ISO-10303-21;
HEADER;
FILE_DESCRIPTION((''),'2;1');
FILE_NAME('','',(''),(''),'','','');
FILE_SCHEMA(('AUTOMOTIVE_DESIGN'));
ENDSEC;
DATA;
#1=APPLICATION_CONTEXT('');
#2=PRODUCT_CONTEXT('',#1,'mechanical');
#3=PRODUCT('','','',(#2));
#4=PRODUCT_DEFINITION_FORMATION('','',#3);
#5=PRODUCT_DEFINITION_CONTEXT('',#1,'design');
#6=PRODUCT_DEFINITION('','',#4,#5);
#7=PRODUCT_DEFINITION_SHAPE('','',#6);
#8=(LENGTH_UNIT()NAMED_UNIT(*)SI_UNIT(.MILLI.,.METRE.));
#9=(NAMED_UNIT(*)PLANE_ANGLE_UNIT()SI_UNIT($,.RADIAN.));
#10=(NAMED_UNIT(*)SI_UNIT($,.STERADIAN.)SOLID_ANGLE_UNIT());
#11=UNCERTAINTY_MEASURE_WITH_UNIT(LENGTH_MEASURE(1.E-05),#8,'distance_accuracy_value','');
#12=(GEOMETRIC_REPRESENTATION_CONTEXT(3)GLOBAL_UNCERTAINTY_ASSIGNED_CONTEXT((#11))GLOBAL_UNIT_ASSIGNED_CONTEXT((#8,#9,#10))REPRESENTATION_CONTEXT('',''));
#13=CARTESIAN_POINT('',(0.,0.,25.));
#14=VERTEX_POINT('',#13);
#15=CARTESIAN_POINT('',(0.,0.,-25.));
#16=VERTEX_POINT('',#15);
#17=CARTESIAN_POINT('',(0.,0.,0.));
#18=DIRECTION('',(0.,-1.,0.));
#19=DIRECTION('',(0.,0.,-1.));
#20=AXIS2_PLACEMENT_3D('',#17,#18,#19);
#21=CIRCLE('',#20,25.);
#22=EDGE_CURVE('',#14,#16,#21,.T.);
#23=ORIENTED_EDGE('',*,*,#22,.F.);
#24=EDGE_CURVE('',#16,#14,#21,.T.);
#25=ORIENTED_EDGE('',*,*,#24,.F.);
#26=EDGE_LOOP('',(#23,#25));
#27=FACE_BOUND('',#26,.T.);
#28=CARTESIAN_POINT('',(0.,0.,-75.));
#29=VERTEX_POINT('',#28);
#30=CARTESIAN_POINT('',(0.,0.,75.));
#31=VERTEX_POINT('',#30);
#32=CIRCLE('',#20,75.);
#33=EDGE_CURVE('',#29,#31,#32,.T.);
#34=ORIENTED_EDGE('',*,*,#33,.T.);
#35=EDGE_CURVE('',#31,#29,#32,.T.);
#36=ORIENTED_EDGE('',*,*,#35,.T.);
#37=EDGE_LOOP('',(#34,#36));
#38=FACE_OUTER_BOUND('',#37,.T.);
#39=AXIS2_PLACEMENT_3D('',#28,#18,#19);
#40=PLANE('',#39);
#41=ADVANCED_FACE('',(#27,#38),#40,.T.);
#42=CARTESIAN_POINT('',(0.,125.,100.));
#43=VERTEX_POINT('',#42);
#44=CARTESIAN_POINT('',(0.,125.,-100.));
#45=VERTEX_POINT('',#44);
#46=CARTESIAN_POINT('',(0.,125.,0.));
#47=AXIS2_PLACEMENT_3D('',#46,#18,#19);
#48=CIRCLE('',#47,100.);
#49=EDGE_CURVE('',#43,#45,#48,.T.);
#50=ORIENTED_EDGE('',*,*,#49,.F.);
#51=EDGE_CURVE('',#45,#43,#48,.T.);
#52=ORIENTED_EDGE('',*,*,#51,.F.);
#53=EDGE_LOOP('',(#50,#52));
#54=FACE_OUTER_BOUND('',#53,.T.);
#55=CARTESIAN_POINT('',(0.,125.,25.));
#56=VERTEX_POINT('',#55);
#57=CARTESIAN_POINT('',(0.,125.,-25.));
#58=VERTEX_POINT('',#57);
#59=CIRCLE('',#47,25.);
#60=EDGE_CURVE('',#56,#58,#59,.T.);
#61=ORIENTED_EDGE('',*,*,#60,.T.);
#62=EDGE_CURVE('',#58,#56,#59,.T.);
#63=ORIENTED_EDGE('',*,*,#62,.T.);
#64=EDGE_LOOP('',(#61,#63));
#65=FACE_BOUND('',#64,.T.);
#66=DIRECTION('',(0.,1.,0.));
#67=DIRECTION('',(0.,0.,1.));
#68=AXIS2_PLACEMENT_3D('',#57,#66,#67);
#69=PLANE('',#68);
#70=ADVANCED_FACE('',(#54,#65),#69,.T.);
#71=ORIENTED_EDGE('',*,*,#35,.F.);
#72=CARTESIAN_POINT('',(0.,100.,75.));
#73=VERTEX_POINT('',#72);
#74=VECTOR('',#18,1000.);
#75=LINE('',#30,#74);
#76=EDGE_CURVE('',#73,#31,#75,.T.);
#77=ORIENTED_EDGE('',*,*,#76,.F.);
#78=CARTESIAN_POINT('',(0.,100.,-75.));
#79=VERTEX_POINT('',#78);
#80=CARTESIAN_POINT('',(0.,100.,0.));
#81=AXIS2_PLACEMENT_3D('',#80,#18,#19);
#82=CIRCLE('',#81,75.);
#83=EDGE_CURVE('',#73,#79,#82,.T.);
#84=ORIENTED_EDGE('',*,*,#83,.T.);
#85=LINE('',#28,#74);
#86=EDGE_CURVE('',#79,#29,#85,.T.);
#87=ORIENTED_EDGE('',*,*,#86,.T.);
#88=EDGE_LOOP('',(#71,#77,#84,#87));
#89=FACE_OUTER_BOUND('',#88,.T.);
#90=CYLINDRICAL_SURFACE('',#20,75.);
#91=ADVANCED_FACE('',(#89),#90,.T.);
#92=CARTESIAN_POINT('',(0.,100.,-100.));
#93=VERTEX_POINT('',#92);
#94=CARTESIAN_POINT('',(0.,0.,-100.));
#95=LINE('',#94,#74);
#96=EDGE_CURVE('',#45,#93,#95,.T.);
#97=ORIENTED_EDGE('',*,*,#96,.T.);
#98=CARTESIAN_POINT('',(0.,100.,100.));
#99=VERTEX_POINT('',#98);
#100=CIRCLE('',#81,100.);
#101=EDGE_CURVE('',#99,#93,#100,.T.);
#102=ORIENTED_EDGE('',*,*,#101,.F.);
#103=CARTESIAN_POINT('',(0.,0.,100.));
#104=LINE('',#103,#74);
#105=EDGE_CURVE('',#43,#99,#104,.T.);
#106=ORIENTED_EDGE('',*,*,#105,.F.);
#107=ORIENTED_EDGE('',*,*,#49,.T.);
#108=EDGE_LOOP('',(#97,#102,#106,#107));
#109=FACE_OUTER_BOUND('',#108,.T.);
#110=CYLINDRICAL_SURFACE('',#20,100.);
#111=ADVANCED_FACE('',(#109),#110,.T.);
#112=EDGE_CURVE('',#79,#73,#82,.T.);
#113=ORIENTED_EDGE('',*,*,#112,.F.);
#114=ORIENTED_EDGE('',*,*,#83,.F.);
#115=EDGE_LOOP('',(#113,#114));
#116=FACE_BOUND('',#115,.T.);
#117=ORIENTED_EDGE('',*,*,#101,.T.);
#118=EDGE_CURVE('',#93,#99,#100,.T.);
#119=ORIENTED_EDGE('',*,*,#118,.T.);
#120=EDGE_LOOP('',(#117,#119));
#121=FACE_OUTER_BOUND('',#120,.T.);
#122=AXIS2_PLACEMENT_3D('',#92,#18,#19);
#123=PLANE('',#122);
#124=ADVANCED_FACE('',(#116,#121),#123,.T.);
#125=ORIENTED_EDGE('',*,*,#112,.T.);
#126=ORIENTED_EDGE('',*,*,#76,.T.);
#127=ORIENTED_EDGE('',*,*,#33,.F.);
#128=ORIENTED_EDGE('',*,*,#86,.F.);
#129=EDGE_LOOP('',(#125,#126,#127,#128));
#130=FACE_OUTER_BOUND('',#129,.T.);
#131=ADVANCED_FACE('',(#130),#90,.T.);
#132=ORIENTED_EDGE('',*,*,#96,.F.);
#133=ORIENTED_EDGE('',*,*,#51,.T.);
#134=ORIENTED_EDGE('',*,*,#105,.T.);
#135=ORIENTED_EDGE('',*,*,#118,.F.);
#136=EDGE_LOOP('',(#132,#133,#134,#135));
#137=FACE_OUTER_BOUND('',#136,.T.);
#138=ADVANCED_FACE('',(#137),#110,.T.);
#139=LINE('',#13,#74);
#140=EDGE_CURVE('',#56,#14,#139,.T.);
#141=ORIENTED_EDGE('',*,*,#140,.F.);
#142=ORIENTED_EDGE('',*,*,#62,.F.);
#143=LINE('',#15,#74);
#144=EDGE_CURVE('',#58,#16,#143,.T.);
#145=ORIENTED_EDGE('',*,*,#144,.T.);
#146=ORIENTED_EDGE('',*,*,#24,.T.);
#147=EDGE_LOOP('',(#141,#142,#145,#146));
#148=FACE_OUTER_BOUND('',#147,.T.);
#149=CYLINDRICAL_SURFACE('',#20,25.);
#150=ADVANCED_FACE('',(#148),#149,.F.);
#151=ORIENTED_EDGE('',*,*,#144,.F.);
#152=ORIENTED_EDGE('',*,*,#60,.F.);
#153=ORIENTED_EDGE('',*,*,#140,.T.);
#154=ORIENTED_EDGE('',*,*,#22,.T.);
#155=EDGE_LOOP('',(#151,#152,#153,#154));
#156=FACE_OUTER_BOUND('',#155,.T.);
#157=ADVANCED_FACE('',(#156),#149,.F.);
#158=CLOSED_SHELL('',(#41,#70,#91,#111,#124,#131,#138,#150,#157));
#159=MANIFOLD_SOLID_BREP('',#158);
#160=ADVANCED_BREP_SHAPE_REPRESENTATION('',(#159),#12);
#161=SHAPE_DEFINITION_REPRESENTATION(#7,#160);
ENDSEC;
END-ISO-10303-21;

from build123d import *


with BuildPart() as part:
    # Bushing Half-Section Profile → Flanged Bushing Body (revolve)
    with BuildSketch(Plane(origin=(0, 0, 0), x_dir=(0, 0, -1), z_dir=(1, 0, 0))):
        Polygon((25, 0), (25, 125), (100, 125), (100, 100), (75, 100), (75, 0), align=None)
    revolve(axis=Axis((0, 0, 0), (0, 1, 0)))


solid = part.part
